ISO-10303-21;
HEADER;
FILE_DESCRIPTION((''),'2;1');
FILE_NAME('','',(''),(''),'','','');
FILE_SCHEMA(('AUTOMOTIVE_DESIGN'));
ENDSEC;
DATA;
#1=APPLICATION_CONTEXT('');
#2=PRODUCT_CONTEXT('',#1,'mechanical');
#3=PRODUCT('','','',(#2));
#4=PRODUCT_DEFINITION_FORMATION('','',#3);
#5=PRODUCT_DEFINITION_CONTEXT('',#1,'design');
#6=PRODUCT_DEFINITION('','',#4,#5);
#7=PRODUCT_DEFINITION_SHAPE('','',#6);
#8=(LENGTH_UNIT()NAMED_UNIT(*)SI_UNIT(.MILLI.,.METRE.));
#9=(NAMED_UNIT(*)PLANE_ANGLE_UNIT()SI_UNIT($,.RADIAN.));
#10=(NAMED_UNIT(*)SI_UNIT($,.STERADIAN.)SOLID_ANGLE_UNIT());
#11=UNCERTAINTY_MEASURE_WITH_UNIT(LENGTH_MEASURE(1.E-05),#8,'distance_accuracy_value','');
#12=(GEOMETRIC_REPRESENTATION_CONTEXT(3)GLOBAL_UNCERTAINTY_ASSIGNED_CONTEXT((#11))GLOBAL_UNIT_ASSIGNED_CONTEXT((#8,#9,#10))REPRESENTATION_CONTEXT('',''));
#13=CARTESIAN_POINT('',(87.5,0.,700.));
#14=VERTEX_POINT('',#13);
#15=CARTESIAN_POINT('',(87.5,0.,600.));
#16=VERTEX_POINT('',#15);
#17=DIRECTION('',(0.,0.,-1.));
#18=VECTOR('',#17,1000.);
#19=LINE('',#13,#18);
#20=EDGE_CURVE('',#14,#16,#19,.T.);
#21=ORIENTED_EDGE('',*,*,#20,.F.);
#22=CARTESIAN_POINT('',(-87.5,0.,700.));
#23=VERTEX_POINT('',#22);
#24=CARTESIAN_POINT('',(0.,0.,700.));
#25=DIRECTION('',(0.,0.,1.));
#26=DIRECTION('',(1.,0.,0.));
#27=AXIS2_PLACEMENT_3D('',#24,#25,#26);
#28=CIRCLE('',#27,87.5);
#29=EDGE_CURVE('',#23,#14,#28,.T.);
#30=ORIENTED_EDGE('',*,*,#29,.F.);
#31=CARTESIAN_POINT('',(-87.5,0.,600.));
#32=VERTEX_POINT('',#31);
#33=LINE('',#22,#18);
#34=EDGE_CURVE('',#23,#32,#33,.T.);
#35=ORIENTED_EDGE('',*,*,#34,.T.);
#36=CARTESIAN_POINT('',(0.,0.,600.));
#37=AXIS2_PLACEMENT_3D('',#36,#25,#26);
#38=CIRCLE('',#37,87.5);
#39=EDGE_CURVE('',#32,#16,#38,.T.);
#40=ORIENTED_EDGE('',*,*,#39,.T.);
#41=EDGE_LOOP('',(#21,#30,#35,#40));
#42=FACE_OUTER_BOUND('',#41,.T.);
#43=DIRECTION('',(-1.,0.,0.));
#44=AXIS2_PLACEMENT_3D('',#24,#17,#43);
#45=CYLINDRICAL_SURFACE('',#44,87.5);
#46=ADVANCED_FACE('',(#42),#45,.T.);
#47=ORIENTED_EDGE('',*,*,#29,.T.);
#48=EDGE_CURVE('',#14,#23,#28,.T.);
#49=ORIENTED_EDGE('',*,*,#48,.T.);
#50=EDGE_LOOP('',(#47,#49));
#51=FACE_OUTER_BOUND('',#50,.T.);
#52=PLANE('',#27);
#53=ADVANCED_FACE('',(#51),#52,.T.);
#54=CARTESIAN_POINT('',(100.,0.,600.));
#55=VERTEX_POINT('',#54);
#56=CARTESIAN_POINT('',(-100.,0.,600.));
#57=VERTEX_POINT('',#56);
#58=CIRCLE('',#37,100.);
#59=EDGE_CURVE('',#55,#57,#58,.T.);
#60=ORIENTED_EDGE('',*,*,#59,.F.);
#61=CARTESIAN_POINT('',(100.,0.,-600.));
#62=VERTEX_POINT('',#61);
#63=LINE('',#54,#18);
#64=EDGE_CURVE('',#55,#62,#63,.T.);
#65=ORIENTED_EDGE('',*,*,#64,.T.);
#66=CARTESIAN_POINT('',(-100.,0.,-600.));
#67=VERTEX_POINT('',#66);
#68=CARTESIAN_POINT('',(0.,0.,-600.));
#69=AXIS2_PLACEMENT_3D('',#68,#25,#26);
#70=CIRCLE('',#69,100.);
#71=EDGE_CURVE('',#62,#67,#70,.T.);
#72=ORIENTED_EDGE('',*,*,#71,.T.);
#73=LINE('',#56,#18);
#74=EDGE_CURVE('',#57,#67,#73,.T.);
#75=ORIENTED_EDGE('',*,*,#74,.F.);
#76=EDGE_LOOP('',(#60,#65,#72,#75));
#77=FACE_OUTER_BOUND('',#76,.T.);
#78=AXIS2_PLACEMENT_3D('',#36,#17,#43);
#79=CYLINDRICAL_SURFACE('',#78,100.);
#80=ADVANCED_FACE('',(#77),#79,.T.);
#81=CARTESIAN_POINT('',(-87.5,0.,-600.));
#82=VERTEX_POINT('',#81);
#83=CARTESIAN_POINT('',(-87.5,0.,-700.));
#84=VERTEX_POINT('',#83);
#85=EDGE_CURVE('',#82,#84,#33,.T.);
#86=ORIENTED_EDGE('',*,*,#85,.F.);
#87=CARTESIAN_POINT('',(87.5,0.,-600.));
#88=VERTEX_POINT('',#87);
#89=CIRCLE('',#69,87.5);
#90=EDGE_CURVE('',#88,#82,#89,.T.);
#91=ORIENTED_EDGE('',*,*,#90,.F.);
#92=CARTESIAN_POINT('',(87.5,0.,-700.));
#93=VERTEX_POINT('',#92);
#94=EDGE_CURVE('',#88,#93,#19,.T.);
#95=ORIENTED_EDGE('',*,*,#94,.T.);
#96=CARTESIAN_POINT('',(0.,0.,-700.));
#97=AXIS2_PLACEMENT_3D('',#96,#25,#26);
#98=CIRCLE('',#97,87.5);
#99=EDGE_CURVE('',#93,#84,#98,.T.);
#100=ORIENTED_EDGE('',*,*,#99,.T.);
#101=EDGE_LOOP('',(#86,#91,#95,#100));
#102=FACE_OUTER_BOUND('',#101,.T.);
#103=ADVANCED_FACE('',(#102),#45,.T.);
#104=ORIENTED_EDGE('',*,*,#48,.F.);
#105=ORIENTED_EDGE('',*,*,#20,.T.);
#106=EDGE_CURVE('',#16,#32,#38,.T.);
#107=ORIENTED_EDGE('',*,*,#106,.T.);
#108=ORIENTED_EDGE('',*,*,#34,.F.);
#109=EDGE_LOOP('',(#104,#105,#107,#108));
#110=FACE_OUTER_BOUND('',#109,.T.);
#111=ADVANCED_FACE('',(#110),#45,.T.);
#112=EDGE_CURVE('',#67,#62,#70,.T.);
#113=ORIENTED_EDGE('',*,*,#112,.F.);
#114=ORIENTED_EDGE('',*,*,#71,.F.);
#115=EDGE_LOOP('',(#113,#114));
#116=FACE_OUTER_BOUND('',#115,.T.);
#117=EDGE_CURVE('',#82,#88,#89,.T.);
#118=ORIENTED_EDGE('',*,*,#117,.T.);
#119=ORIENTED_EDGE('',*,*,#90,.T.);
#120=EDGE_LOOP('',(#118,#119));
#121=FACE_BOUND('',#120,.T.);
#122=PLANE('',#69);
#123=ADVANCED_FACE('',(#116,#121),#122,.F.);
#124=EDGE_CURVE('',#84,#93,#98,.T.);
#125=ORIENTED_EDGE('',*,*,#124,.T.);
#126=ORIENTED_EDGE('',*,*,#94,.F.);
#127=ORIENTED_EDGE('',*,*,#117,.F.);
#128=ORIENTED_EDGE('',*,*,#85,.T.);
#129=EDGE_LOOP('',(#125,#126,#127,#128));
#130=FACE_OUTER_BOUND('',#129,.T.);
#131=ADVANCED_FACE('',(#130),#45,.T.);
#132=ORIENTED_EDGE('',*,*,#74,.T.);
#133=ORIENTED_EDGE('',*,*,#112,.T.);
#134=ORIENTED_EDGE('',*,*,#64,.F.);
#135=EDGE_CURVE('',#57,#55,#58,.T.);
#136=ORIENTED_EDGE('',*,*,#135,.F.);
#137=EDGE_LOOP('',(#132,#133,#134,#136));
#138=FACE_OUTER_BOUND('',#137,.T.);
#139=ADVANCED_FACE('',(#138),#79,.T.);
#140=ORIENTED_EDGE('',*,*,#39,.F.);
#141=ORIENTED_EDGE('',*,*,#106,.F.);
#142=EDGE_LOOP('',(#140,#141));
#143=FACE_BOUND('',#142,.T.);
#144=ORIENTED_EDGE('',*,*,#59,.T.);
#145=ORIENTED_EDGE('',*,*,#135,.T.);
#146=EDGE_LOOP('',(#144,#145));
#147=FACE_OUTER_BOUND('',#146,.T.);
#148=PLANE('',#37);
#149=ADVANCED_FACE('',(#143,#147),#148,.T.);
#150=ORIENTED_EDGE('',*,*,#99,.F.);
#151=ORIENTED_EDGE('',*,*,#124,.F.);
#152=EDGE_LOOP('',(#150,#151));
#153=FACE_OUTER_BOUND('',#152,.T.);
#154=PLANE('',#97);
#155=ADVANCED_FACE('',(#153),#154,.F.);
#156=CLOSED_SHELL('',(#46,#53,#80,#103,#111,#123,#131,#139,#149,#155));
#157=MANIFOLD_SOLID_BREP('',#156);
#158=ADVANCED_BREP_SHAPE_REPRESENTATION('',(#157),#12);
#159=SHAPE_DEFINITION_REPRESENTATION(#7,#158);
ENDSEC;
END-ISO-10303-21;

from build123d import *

# Parameters (mm, degrees)
SKETCH1_R           = 87.5
BOSS_EXTRUDE1_DEPTH = 700
SKETCH2_R           = 100
BOSS_EXTRUDE2_DEPTH = 600


with BuildPart() as part:
    # Sketch1 → Boss-Extrude1 (new, symmetric)
    with BuildSketch(Plane.XY):
        Circle(SKETCH1_R)
    extrude(amount=BOSS_EXTRUDE1_DEPTH, both=True)

    # Sketch2 → Boss-Extrude2 (add, symmetric)
    with BuildSketch(Plane.XY):
        Circle(SKETCH2_R)
    extrude(amount=BOSS_EXTRUDE2_DEPTH, both=True)


solid = part.part
